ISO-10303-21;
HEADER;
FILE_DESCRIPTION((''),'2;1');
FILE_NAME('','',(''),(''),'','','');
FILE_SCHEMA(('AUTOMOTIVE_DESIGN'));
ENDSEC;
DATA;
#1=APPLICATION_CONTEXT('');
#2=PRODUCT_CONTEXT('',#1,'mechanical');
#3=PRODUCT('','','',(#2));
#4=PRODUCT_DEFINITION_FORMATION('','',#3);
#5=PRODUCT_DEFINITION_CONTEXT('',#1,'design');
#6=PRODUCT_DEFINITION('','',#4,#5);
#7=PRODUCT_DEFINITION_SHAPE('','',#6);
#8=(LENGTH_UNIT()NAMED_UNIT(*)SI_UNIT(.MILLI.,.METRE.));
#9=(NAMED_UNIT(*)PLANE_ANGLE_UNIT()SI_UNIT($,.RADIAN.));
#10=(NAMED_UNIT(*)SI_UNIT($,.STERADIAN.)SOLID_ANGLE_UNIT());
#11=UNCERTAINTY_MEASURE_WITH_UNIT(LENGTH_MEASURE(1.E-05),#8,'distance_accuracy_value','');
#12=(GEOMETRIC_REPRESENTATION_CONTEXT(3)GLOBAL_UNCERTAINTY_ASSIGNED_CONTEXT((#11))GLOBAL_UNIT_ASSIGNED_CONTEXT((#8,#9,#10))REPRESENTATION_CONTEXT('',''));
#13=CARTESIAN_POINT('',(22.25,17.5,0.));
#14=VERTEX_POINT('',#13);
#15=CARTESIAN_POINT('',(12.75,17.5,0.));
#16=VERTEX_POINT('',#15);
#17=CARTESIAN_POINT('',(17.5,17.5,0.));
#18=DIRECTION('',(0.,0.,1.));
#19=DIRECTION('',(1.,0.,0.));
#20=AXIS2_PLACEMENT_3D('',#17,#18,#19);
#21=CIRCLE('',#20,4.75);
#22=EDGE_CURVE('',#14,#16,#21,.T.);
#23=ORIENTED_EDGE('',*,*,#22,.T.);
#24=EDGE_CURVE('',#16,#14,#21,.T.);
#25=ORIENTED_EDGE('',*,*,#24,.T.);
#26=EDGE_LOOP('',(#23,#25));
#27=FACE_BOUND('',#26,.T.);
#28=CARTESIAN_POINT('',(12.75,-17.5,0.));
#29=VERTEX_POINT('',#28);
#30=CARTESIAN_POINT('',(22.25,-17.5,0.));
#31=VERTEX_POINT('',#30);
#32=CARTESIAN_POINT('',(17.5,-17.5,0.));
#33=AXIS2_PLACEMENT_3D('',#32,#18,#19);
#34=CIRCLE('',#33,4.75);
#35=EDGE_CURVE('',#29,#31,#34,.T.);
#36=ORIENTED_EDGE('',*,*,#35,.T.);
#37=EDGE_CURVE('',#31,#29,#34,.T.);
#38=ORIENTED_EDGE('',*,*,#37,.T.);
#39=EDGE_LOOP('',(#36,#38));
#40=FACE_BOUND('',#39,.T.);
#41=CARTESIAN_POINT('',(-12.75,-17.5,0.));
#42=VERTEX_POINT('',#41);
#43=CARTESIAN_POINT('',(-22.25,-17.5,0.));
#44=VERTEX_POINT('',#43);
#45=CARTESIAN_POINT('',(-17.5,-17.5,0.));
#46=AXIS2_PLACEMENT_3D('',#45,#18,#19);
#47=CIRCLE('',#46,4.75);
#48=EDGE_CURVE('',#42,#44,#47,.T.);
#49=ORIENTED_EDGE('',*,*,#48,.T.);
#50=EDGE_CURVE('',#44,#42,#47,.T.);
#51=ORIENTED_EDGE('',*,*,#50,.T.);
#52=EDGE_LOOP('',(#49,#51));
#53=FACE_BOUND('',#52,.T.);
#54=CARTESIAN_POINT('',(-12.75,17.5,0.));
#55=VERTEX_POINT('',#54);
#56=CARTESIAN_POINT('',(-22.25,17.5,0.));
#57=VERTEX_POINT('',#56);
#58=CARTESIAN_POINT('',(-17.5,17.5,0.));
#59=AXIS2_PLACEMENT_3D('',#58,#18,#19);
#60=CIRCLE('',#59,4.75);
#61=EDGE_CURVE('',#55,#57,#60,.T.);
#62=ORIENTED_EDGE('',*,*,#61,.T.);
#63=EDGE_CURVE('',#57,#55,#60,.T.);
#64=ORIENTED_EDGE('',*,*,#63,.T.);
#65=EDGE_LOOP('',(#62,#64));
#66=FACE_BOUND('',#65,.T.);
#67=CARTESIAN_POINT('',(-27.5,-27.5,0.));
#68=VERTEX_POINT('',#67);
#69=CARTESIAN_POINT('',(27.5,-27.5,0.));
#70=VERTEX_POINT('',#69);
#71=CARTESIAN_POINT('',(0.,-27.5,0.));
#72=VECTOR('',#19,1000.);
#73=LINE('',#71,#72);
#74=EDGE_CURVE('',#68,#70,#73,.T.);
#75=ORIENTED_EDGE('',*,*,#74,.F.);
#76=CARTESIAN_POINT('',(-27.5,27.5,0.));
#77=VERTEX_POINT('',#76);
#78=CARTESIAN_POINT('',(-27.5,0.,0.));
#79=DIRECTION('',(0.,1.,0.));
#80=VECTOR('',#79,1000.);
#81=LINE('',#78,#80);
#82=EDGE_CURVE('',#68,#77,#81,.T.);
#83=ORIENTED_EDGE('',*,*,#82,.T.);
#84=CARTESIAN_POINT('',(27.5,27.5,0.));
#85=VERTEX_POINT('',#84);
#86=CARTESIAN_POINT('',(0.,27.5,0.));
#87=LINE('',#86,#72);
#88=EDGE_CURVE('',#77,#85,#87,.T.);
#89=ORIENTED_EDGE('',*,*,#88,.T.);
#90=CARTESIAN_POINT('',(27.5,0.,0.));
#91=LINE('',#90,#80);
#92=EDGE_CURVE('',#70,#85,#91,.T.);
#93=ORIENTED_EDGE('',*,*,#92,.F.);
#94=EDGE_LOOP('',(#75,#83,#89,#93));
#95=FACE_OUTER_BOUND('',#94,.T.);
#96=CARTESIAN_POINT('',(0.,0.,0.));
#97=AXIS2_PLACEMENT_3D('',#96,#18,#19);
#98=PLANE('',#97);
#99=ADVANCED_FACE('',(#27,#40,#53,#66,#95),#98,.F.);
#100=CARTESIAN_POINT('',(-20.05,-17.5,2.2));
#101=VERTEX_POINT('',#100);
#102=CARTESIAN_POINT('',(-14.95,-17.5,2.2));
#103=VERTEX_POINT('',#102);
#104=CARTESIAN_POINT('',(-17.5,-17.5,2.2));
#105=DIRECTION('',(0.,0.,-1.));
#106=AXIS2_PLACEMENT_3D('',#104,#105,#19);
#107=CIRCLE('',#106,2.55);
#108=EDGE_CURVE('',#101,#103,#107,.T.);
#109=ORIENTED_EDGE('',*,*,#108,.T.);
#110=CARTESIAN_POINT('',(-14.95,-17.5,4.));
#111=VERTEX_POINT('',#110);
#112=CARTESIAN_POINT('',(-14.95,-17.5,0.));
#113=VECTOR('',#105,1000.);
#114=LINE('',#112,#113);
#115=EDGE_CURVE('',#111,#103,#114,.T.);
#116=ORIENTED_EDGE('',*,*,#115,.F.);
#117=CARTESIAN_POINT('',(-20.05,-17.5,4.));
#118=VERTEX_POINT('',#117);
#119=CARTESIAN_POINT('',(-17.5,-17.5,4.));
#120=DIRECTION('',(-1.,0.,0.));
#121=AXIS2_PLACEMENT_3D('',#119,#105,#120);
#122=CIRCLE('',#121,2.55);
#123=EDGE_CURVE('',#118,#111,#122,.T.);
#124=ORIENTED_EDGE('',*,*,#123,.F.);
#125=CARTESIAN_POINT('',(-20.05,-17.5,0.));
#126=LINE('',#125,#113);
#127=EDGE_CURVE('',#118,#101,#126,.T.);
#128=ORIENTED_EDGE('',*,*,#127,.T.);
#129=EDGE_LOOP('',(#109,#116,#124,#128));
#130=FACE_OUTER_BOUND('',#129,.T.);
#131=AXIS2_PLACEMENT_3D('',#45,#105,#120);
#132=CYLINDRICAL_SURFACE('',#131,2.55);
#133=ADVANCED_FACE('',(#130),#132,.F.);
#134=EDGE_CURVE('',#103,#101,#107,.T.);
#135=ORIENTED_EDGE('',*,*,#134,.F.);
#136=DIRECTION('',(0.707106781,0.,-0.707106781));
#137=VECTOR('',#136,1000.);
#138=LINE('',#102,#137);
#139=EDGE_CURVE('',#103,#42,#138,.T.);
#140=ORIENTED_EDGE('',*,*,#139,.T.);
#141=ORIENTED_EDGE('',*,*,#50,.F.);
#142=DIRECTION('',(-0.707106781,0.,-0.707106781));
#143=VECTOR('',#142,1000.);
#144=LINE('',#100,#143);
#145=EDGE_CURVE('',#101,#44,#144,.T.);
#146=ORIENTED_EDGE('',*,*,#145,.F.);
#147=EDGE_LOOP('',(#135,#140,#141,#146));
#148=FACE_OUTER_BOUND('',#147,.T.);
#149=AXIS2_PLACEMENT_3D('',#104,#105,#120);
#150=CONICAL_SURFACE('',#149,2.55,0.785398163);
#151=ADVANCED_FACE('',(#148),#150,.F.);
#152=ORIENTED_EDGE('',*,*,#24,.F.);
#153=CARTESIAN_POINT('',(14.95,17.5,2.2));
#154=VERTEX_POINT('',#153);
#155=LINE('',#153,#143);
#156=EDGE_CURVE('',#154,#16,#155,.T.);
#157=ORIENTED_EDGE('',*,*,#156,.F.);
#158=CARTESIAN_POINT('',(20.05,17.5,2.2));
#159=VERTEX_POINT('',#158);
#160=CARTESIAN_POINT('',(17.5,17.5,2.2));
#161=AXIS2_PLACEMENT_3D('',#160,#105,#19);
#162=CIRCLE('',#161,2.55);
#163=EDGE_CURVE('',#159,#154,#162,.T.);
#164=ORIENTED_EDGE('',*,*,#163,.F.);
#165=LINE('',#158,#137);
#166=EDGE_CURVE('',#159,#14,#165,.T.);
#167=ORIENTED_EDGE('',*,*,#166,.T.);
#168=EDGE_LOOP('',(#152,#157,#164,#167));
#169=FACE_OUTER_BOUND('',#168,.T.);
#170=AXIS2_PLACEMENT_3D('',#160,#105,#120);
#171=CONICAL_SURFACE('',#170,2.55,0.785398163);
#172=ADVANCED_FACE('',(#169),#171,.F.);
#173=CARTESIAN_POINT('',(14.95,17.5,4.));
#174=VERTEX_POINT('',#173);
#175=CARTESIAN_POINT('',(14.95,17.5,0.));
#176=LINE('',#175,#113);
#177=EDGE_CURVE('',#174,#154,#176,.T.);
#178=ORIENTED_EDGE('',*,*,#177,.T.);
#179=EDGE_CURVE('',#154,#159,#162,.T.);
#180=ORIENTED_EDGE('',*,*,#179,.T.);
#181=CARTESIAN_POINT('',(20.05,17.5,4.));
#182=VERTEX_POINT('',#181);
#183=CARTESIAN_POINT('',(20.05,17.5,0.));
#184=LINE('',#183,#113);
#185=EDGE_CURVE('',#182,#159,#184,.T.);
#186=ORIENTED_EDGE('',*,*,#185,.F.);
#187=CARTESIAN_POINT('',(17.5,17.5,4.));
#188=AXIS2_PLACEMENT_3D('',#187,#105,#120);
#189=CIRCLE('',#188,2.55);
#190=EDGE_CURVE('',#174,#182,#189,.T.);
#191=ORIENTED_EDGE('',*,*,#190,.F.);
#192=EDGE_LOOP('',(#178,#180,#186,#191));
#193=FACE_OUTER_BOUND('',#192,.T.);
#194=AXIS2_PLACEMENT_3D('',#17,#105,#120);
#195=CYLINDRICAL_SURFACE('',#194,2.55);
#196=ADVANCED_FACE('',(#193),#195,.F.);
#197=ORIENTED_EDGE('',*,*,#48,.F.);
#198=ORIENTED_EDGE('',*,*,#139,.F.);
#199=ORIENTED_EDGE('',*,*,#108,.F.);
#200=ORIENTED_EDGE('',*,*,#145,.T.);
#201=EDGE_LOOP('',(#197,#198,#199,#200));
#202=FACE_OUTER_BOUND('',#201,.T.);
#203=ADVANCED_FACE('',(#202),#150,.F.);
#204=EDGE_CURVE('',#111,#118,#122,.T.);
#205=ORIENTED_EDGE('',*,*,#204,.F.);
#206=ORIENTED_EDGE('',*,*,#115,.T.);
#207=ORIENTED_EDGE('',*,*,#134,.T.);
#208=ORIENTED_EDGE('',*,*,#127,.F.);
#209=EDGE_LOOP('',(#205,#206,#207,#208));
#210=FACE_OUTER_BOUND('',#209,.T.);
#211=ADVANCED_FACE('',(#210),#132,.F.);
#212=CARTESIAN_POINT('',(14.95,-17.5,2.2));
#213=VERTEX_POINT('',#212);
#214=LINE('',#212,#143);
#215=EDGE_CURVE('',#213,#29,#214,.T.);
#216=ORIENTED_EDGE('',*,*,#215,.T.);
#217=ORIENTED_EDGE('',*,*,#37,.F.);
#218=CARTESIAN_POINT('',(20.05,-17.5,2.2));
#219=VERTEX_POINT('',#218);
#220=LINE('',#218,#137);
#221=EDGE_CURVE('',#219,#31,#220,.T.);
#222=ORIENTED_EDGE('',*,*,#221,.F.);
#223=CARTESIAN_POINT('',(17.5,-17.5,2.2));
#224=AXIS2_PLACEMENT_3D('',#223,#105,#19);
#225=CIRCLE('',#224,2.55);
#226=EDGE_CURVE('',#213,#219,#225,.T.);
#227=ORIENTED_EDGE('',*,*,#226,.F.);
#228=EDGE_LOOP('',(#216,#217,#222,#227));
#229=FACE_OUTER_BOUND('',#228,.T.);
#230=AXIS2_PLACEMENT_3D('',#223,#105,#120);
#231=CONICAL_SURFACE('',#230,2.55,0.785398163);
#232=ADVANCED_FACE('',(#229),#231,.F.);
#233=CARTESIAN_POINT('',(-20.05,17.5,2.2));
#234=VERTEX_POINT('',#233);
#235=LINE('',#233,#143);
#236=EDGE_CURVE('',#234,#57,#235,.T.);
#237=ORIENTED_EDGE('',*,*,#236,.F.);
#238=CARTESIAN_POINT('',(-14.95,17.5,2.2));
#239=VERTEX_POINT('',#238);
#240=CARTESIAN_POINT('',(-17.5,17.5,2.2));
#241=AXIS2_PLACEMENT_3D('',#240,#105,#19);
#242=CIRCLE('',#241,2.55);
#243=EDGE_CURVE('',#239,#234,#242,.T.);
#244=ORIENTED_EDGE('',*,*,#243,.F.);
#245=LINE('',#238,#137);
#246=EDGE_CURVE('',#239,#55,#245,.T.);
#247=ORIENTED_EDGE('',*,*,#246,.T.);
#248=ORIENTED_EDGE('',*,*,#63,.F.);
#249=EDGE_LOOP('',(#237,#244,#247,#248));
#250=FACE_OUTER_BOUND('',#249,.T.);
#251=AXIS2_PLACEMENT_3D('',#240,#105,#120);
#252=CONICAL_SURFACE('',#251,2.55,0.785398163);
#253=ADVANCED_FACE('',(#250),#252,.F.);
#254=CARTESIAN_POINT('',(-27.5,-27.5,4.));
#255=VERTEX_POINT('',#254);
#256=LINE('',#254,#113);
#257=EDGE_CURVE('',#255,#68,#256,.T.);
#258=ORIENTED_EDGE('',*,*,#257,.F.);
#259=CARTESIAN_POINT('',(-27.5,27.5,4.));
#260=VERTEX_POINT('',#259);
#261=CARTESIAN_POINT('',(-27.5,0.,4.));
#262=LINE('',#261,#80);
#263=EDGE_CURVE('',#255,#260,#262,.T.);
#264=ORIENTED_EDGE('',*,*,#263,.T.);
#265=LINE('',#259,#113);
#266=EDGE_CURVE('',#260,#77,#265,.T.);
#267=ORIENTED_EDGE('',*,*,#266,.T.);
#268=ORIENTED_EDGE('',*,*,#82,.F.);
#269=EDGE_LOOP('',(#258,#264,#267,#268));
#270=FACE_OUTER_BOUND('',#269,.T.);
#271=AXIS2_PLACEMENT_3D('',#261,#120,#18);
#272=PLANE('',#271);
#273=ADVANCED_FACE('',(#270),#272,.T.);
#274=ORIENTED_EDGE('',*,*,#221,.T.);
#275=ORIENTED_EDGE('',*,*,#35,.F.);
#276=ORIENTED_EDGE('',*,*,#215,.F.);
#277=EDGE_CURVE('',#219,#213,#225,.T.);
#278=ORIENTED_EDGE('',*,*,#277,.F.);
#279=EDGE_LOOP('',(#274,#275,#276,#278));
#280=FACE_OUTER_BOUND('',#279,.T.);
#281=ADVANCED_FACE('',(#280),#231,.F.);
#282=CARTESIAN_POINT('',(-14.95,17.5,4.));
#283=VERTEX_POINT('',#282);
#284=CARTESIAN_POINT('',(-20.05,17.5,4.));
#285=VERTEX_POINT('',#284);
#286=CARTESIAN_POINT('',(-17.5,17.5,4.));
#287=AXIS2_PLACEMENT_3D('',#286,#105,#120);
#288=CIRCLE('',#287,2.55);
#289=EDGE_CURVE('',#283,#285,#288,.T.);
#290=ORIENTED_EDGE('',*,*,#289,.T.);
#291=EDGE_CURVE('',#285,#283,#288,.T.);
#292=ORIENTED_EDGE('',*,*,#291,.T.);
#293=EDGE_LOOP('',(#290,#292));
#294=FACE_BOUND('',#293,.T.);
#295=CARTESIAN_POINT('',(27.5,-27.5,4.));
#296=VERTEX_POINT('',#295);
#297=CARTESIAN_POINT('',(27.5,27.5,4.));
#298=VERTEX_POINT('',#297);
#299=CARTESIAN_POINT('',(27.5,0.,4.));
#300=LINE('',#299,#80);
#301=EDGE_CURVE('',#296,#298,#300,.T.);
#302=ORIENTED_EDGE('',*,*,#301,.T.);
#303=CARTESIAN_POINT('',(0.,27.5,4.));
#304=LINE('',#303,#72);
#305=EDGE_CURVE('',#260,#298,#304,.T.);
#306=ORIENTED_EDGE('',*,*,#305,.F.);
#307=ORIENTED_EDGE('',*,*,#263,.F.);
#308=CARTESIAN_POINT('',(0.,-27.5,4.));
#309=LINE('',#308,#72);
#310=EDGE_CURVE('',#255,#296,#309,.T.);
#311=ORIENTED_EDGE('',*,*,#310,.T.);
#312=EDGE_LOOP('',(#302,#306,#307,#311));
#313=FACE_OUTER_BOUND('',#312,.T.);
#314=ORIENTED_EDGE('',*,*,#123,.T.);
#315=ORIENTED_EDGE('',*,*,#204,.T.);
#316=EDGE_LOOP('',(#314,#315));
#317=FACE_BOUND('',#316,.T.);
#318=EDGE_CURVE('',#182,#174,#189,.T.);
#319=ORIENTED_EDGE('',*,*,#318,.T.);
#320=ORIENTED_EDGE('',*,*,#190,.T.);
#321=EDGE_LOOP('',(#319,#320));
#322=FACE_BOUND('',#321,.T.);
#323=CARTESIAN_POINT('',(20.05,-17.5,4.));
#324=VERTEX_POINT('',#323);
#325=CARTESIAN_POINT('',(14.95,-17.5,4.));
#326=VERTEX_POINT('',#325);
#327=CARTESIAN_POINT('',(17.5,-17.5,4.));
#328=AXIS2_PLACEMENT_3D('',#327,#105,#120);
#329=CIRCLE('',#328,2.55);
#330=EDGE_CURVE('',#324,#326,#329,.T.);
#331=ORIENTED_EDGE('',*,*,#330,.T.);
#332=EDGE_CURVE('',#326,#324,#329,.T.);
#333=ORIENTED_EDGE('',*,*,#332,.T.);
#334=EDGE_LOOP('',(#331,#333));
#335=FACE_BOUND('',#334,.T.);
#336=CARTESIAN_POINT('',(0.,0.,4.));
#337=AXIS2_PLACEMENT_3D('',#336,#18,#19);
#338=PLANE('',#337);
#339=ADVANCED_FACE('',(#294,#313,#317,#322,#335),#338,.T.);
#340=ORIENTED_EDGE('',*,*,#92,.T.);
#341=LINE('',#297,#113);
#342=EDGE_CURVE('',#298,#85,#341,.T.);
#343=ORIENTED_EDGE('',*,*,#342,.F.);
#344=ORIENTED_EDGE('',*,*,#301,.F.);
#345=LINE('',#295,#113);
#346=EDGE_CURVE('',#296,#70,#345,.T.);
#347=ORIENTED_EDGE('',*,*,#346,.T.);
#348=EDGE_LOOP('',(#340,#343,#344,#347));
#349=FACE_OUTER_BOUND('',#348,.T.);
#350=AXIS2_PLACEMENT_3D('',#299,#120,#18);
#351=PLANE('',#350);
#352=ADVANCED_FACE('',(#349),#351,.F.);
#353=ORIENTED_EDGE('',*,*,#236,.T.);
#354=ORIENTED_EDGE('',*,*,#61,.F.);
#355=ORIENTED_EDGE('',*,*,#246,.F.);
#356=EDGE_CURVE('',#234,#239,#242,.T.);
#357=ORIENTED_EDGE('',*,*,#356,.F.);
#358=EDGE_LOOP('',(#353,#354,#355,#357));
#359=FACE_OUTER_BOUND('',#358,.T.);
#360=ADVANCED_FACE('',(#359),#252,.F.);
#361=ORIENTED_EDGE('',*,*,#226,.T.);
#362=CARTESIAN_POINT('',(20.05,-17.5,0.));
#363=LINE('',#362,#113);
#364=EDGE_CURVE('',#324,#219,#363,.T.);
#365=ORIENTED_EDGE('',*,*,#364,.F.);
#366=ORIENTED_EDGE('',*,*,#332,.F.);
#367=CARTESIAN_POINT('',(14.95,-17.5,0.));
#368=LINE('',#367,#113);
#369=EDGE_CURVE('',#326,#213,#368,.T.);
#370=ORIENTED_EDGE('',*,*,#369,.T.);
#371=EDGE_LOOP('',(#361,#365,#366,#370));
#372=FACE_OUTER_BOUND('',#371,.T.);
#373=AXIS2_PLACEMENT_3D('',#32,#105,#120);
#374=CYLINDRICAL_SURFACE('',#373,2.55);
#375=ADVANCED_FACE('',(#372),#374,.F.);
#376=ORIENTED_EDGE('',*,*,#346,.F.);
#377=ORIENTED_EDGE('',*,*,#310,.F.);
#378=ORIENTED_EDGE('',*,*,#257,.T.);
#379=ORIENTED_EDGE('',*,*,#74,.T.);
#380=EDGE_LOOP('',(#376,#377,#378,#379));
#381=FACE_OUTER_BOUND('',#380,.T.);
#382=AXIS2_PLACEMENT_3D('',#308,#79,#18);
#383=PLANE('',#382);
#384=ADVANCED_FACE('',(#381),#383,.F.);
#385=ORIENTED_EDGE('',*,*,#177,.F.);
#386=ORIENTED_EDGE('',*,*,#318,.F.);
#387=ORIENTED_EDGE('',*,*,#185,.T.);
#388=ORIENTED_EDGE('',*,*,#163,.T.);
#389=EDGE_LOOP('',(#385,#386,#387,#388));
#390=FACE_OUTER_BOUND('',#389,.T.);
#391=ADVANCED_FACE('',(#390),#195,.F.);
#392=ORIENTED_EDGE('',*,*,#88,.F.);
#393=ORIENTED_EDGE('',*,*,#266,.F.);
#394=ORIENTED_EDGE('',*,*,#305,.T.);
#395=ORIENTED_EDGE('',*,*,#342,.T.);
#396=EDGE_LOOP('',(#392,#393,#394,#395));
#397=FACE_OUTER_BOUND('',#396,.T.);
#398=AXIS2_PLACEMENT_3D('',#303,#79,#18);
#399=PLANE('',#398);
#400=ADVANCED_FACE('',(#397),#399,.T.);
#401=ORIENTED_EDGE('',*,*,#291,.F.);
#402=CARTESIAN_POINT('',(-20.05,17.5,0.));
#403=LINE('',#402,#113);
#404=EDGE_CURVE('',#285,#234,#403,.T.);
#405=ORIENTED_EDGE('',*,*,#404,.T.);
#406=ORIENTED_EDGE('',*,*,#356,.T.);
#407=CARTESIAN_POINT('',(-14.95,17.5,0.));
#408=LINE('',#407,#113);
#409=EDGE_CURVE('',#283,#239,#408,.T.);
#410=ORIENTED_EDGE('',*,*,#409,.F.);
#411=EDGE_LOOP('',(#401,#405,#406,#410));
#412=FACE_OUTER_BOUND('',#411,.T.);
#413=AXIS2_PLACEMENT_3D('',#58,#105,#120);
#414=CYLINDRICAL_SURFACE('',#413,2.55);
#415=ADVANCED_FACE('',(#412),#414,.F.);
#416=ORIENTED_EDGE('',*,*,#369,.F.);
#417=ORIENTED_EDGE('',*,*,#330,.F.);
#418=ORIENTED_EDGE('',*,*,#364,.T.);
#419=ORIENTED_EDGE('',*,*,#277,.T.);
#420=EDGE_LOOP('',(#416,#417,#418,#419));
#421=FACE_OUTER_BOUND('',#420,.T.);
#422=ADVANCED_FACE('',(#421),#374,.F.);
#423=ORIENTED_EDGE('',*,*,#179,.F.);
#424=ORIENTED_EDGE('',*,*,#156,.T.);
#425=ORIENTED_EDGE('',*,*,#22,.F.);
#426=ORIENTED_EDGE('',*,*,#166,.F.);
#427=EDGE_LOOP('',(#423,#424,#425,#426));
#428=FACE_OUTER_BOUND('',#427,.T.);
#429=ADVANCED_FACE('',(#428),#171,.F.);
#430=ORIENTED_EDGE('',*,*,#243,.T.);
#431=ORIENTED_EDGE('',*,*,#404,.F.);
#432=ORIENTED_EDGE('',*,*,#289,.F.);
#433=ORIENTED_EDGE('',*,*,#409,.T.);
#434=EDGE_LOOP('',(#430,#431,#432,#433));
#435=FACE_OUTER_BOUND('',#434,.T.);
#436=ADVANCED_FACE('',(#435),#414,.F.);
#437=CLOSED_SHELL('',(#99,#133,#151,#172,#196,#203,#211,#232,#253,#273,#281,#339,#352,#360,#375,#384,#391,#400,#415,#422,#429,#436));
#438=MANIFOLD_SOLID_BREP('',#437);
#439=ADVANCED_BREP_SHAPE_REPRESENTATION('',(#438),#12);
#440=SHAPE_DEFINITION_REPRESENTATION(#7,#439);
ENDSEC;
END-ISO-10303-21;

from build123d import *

# Parameters (mm, degrees)
SKETCH1_W                  = 55
SKETCH1_H                  = 55
SKETCH1_W_2                = 35
SKETCH1_H_2                = 35
BOSS_EXTRUDE1_DEPTH        = 4
F_1_0_5_1_DIAMETER_HOLE1_D = 5.1
CHAMFER1_SIZE              = 2.2


with BuildPart() as part:
    # Sketch1 → Boss-Extrude1 (new body)
    # profile 1 of 2: a face of its own
    with BuildSketch(Plane.XY):
        Rectangle(SKETCH1_W, SKETCH1_H)
        Rectangle(SKETCH1_W_2, SKETCH1_H_2, mode=Mode.SUBTRACT)
    # profile 2 of 2: a face of its own
    with BuildSketch(Plane.XY):
        Rectangle(SKETCH1_W_2, SKETCH1_H_2)
    extrude(amount=BOSS_EXTRUDE1_DEPTH)

    # Ø1.0 (5.1) Diameter Hole1 (through all)
    with Locations(Plane(origin=(0, 0, 0), x_dir=(-1, 0, 0), z_dir=(0, 0, -1))):
        with Locations((-17.5, 17.5), (17.5, 17.5), (17.5, -17.5), (-17.5, -17.5)):
            Hole(F_1_0_5_1_DIAMETER_HOLE1_D / 2)

    # Chamfer1
    chamfer1_edges = [part.edges().sort_by_distance(p)[0] for p in [
        (14.95, -17.5, 0),
        (-20.05, -17.5, 0),
        (-20.05, 17.5, 0),
        (14.95, 17.5, 0),
    ]]
    chamfer(chamfer1_edges, length=CHAMFER1_SIZE)


solid = part.part
